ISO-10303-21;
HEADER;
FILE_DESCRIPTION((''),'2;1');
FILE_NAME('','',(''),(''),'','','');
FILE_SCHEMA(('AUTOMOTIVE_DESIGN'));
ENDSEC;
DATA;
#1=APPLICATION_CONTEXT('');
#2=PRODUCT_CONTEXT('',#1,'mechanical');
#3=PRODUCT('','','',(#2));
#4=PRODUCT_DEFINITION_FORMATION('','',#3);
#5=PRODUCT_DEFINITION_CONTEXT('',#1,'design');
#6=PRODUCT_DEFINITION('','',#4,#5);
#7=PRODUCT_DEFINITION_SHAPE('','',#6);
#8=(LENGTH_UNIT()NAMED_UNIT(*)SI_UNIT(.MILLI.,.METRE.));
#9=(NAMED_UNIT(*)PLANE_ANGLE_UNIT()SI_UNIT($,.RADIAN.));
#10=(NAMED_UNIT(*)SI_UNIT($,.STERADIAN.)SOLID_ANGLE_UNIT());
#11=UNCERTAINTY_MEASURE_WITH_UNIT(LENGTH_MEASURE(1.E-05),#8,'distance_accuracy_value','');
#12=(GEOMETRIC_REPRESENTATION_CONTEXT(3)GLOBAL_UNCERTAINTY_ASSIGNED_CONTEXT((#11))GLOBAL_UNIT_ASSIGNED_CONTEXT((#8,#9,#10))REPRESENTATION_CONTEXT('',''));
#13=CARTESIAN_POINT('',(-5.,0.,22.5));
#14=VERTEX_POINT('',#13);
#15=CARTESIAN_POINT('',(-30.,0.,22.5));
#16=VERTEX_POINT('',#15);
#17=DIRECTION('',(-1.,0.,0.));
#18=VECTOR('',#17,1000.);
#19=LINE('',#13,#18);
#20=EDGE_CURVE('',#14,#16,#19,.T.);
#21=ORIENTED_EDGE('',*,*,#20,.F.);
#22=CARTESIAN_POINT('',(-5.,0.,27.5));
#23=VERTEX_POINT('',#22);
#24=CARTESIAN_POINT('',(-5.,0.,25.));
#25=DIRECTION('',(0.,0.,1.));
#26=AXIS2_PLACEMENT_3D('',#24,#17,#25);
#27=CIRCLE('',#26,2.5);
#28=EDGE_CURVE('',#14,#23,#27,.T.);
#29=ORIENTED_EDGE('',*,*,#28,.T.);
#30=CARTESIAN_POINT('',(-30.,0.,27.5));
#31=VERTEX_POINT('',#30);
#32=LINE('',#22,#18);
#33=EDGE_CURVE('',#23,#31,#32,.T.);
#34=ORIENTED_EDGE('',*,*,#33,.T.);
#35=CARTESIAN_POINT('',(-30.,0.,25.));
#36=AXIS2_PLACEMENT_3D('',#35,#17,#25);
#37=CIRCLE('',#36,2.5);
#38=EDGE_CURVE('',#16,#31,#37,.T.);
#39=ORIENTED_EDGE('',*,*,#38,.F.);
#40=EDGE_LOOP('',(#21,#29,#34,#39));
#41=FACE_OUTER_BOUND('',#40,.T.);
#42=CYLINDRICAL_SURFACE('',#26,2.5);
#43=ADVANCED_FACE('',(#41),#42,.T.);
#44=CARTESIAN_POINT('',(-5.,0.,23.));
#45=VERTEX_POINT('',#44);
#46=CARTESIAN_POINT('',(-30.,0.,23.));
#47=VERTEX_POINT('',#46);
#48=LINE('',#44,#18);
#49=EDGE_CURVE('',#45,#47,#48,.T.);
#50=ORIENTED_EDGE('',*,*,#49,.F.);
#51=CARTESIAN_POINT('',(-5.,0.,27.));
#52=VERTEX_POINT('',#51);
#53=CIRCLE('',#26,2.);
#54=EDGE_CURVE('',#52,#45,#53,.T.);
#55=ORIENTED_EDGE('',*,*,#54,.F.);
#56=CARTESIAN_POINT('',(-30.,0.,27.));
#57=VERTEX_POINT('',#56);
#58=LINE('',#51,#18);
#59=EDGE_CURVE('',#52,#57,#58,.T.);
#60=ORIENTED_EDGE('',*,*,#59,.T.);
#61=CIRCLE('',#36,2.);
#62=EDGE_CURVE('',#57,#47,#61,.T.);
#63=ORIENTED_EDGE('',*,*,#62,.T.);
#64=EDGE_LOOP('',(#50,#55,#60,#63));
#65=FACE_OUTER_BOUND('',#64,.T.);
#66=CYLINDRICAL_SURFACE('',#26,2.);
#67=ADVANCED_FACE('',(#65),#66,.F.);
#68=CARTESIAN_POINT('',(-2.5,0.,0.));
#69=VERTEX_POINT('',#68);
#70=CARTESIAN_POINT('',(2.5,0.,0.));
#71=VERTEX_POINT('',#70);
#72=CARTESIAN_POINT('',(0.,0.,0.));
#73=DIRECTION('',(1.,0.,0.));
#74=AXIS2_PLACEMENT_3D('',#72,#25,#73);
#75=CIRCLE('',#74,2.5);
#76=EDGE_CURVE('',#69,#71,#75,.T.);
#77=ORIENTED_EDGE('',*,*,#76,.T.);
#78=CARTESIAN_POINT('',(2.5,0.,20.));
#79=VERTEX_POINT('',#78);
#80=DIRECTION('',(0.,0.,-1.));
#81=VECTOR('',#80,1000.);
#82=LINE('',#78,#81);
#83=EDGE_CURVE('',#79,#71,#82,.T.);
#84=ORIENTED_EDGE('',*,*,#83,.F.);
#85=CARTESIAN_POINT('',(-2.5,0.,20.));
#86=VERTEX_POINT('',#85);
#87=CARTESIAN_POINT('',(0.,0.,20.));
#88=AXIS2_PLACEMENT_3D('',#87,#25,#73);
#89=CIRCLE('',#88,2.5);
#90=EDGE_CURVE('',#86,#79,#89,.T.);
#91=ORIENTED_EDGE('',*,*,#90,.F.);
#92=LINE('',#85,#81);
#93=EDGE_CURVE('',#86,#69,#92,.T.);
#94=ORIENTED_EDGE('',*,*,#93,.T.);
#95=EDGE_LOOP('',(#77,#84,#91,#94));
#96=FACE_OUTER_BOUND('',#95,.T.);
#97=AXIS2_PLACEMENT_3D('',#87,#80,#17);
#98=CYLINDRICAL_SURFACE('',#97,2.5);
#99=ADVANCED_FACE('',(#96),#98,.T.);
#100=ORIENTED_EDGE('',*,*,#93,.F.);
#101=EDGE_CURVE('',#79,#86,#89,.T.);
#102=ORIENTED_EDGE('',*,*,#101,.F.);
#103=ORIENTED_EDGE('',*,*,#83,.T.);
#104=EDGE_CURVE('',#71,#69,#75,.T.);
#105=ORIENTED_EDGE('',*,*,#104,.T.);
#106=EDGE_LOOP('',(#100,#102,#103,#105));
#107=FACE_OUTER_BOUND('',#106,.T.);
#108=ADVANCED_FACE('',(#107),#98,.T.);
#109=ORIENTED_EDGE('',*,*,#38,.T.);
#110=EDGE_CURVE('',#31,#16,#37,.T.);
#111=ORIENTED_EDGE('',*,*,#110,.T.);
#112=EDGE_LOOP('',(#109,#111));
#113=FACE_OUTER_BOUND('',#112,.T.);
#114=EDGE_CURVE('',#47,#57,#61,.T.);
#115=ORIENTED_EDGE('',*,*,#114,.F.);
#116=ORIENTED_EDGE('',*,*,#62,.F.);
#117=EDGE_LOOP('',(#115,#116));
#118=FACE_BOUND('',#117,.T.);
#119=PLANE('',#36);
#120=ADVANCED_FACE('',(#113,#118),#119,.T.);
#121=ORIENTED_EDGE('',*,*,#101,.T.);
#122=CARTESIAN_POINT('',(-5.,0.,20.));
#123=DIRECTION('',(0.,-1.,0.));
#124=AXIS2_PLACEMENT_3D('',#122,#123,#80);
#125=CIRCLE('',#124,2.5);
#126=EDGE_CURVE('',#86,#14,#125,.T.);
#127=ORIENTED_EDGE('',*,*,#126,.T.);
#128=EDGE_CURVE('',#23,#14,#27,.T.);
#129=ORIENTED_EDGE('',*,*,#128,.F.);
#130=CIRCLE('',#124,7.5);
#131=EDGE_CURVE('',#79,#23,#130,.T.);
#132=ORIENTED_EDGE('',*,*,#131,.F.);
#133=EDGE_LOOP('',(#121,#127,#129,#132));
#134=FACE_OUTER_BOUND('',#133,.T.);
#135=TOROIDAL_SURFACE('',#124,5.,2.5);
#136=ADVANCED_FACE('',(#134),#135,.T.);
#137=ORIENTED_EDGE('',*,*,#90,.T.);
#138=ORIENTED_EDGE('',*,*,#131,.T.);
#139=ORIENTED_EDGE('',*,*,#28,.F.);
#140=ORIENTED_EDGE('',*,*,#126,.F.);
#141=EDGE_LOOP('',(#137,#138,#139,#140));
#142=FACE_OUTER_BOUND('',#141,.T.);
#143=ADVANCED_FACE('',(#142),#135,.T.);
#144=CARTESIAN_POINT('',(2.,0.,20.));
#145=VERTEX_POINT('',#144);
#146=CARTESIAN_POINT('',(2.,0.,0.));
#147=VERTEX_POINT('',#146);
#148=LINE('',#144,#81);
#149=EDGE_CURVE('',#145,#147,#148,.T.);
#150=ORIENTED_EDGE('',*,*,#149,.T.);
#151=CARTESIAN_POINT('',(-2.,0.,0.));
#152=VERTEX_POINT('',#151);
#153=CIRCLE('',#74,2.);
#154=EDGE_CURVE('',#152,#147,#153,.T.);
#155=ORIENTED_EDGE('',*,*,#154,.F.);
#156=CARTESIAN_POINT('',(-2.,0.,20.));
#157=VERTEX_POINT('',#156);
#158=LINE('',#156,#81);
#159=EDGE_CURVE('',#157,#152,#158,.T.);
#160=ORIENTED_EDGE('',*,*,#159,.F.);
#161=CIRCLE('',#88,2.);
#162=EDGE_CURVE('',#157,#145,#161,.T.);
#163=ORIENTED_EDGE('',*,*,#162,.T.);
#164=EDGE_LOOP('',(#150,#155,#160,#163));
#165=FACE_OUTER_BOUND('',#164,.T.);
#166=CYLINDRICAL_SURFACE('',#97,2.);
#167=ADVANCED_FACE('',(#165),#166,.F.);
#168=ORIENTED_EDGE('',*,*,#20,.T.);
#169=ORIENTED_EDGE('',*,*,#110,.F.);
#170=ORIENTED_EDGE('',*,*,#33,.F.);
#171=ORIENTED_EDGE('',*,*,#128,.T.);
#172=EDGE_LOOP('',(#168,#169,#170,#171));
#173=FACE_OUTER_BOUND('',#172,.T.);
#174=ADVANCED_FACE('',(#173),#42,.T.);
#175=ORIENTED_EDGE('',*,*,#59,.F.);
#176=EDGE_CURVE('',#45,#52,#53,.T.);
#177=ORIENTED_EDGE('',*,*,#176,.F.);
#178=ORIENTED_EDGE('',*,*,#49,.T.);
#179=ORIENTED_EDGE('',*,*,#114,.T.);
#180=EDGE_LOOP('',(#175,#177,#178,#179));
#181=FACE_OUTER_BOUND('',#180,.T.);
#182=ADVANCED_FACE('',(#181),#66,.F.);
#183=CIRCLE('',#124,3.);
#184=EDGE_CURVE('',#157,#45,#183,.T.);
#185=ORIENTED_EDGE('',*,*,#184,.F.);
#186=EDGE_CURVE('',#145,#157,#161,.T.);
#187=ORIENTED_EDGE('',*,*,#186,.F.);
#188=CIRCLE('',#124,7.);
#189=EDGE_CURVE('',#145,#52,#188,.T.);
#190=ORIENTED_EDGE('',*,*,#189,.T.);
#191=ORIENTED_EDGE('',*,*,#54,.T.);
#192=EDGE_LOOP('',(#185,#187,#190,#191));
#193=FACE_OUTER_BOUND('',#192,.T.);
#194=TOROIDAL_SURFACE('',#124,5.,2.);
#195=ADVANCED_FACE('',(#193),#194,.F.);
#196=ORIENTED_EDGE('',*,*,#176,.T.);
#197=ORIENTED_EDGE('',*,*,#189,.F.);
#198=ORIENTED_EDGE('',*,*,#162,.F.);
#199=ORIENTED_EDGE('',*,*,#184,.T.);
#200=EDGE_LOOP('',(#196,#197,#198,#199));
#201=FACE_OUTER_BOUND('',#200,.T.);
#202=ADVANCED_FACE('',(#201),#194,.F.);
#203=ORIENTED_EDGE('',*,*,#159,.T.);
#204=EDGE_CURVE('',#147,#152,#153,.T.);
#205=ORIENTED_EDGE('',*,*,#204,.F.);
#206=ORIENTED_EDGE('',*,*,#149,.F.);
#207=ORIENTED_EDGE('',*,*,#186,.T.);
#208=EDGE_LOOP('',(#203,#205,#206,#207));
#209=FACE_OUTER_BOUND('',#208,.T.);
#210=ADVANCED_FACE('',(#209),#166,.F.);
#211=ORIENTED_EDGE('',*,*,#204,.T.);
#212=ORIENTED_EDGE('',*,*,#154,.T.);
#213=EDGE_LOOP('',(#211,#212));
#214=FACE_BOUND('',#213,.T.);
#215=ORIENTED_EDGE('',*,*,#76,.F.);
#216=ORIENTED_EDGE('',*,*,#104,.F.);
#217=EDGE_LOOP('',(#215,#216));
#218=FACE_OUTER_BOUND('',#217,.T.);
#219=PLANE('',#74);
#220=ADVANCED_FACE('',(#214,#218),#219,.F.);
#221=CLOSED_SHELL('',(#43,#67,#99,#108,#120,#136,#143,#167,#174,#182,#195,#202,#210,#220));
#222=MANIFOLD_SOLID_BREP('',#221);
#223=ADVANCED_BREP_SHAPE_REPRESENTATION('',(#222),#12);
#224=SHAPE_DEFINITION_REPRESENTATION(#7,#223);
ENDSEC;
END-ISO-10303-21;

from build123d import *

# Parameters (mm, degrees)
SKETCH1_R   = 2.5
SKETCH1_R_2 = 2


with BuildPart() as part:
    # Sweep1: sweep along a path in Sketch2
    with BuildLine(Plane(origin=(0, 0, 0), x_dir=(1, 0, 0), z_dir=(0, 1, 0))) as sweep1_path:
        Line((0, 0), (0, -20))
        ThreePointArc((0, -20), (-1.464466094, -23.535533906), (-5, -25))
        Line((-5, -25), (-30, -25))
    # Sketch1 → Sweep1 (sweep)
    with BuildSketch(Plane.XY):
        Circle(SKETCH1_R)
        Circle(SKETCH1_R_2, mode=Mode.SUBTRACT)
    sweep(path=sweep1_path.line)


solid = part.part
